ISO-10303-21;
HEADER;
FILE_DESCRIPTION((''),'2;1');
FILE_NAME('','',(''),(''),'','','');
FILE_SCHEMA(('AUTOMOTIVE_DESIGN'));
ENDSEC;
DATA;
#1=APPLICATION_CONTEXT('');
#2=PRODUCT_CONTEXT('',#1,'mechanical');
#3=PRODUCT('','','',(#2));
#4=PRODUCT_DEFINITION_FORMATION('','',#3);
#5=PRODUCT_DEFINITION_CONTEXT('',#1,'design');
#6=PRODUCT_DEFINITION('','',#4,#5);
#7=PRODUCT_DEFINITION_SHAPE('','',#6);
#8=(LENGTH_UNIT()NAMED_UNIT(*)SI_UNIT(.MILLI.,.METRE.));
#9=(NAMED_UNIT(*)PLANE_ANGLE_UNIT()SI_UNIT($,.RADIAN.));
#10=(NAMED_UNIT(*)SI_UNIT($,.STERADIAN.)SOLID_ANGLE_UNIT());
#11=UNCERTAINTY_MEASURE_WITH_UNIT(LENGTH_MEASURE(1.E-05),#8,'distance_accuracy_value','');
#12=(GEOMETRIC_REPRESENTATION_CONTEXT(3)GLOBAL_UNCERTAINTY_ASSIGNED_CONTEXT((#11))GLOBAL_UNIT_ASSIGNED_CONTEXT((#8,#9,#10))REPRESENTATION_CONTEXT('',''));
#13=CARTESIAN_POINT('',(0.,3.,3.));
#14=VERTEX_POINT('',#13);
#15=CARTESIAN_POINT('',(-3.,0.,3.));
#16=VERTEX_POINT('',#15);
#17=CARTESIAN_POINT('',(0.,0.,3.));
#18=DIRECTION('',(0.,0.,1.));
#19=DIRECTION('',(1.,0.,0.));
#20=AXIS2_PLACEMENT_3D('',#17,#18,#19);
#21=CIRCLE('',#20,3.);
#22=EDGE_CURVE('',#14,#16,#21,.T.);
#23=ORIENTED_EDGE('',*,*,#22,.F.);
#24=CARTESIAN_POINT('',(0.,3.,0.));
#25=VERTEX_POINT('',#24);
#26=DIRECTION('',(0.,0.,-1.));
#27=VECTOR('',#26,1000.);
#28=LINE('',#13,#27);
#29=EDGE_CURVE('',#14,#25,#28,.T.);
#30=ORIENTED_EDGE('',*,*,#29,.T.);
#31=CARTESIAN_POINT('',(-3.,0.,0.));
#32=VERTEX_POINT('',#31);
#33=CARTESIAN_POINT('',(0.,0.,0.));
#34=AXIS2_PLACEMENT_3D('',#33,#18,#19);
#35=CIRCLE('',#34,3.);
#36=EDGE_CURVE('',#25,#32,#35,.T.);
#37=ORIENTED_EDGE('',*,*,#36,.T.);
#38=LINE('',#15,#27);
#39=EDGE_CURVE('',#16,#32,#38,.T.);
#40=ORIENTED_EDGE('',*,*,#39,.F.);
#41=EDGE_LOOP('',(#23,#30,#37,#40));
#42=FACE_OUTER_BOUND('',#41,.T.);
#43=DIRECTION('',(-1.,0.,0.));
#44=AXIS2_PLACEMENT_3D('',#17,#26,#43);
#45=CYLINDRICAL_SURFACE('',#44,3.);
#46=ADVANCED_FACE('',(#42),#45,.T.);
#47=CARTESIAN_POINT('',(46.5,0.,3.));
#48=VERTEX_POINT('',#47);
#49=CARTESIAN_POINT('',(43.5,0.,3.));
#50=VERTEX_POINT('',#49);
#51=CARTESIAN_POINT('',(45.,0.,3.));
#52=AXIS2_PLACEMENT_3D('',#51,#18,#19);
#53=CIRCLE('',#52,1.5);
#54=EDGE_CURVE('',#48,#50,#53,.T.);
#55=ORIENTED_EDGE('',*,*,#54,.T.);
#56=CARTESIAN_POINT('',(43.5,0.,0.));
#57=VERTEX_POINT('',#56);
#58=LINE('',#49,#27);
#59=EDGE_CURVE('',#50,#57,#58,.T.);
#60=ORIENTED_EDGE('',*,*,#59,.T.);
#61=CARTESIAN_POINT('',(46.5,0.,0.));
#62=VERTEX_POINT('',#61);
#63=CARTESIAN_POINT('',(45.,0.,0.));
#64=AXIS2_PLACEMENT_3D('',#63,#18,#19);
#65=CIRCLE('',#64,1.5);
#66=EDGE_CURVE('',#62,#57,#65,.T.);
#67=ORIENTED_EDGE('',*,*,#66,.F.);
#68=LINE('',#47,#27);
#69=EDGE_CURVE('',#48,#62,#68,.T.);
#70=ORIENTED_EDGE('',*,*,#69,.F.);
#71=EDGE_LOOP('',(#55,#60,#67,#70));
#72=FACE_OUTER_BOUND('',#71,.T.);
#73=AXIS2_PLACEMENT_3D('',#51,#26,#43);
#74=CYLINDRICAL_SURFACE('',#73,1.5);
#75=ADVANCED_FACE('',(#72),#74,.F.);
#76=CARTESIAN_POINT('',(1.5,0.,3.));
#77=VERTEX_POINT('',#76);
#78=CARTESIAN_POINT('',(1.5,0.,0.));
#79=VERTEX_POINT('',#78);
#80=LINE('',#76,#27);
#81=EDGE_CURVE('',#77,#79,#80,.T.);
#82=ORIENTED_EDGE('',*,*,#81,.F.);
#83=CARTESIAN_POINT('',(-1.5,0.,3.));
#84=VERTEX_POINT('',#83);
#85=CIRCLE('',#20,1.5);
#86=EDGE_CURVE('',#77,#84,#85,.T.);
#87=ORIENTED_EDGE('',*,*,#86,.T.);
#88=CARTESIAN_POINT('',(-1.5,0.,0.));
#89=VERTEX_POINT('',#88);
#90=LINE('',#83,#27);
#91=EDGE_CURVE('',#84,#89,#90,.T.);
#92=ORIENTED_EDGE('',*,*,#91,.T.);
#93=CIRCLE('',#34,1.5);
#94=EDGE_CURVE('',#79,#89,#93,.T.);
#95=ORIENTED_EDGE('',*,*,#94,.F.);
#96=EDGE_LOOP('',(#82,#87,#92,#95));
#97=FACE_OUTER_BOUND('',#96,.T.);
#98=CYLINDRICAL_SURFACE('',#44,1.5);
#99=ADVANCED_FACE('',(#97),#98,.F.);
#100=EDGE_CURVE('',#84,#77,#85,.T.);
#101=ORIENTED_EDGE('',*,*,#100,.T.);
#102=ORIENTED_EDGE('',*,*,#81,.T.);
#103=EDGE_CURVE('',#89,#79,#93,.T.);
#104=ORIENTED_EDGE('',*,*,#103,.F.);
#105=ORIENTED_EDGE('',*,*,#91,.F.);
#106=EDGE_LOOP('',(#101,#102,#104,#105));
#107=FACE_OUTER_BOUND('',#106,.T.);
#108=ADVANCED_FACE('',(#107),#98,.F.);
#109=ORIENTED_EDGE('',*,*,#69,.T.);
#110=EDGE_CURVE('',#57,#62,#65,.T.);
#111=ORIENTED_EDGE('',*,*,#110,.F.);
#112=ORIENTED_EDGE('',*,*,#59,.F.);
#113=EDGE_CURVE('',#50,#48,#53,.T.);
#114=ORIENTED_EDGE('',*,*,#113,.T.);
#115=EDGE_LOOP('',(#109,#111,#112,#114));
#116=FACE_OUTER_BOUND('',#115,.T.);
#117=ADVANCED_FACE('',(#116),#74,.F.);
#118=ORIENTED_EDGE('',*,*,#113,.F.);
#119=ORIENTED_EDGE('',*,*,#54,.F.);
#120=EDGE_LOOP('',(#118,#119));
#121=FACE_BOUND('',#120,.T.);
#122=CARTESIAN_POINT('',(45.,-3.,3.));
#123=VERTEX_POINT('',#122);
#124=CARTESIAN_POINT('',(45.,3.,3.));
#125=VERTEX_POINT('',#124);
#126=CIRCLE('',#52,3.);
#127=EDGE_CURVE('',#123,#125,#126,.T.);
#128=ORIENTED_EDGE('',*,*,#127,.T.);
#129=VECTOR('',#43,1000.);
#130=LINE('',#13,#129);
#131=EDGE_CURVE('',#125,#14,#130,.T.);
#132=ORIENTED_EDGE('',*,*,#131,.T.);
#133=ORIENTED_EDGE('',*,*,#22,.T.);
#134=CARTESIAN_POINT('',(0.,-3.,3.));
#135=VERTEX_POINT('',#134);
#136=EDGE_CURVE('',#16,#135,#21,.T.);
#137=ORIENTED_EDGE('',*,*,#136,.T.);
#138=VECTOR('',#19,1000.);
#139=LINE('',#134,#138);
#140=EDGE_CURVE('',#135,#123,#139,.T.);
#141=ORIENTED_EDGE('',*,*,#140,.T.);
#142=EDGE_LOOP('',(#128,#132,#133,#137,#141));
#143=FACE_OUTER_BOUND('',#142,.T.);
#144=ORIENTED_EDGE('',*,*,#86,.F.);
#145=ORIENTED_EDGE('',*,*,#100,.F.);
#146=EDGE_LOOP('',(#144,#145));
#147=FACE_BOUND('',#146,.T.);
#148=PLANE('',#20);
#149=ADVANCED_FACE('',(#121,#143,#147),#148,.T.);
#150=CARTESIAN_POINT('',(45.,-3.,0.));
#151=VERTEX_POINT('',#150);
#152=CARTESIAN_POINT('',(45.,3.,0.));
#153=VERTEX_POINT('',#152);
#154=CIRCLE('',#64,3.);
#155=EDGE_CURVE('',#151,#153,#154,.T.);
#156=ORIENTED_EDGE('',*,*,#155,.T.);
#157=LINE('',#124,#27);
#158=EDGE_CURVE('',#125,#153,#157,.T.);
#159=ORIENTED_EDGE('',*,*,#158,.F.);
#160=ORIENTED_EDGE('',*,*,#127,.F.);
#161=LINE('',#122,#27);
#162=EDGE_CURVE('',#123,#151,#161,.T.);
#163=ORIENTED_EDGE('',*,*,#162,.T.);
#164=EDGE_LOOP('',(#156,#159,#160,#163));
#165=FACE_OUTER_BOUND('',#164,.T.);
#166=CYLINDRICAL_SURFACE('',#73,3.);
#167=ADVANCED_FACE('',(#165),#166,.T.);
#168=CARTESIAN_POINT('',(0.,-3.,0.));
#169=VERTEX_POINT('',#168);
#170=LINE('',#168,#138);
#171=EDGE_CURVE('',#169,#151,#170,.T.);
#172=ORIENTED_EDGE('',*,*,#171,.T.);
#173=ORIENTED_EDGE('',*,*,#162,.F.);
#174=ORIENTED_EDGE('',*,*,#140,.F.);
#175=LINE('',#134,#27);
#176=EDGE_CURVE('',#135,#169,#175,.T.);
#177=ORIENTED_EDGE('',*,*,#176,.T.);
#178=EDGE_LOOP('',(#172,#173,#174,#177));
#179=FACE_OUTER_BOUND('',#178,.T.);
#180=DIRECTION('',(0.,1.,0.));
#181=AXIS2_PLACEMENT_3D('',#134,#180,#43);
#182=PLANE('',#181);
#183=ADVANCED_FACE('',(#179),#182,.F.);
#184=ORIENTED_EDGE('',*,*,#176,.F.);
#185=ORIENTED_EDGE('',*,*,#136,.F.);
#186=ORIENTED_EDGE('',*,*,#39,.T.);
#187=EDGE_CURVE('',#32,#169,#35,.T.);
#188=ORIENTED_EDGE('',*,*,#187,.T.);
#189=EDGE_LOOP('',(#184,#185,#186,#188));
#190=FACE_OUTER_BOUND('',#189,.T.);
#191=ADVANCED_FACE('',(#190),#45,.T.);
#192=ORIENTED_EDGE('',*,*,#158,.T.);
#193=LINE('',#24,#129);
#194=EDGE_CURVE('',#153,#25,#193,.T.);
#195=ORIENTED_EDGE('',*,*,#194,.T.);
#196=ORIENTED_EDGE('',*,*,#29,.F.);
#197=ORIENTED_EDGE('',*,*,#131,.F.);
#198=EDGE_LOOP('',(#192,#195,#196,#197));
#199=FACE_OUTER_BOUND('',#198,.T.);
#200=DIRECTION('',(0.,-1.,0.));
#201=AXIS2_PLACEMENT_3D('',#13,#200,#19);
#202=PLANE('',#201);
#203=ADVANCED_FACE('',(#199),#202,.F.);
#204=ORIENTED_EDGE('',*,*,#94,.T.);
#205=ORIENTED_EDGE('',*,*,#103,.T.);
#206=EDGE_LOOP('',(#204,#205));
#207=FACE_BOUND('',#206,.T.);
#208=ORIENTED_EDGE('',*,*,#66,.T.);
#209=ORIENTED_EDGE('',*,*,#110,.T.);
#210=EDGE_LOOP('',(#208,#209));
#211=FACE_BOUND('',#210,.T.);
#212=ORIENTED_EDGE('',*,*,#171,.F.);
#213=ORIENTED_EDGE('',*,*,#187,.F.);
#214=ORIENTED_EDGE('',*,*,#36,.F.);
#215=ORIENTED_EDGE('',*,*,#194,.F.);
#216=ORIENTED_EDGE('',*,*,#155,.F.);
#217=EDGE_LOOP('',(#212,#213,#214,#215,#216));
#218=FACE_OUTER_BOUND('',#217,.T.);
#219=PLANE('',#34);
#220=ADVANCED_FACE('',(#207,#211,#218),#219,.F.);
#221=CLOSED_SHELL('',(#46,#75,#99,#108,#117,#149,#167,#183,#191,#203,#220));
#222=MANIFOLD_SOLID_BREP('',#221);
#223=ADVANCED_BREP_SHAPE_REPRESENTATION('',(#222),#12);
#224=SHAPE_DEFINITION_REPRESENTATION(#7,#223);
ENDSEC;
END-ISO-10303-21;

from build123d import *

# Parameters (mm, degrees)
SKETCH1_R           = 1.5
BOSS_EXTRUDE1_DEPTH = 3


with BuildPart() as part:
    # Sketch1 → Boss-Extrude1 (new body)
    with BuildSketch(Plane.XY):
        with BuildLine():
            Line((0, 3), (45, 3))
            ThreePointArc((45, 3), (48, 0), (45, -3))
            Line((45, -3), (0, -3))
            ThreePointArc((0, -3), (-3, 0), (0, 3))
        make_face()
        Circle(SKETCH1_R, mode=Mode.SUBTRACT)
        with Locations((45, 0)):
            Circle(SKETCH1_R, mode=Mode.SUBTRACT)
    extrude(amount=BOSS_EXTRUDE1_DEPTH)


solid = part.part
